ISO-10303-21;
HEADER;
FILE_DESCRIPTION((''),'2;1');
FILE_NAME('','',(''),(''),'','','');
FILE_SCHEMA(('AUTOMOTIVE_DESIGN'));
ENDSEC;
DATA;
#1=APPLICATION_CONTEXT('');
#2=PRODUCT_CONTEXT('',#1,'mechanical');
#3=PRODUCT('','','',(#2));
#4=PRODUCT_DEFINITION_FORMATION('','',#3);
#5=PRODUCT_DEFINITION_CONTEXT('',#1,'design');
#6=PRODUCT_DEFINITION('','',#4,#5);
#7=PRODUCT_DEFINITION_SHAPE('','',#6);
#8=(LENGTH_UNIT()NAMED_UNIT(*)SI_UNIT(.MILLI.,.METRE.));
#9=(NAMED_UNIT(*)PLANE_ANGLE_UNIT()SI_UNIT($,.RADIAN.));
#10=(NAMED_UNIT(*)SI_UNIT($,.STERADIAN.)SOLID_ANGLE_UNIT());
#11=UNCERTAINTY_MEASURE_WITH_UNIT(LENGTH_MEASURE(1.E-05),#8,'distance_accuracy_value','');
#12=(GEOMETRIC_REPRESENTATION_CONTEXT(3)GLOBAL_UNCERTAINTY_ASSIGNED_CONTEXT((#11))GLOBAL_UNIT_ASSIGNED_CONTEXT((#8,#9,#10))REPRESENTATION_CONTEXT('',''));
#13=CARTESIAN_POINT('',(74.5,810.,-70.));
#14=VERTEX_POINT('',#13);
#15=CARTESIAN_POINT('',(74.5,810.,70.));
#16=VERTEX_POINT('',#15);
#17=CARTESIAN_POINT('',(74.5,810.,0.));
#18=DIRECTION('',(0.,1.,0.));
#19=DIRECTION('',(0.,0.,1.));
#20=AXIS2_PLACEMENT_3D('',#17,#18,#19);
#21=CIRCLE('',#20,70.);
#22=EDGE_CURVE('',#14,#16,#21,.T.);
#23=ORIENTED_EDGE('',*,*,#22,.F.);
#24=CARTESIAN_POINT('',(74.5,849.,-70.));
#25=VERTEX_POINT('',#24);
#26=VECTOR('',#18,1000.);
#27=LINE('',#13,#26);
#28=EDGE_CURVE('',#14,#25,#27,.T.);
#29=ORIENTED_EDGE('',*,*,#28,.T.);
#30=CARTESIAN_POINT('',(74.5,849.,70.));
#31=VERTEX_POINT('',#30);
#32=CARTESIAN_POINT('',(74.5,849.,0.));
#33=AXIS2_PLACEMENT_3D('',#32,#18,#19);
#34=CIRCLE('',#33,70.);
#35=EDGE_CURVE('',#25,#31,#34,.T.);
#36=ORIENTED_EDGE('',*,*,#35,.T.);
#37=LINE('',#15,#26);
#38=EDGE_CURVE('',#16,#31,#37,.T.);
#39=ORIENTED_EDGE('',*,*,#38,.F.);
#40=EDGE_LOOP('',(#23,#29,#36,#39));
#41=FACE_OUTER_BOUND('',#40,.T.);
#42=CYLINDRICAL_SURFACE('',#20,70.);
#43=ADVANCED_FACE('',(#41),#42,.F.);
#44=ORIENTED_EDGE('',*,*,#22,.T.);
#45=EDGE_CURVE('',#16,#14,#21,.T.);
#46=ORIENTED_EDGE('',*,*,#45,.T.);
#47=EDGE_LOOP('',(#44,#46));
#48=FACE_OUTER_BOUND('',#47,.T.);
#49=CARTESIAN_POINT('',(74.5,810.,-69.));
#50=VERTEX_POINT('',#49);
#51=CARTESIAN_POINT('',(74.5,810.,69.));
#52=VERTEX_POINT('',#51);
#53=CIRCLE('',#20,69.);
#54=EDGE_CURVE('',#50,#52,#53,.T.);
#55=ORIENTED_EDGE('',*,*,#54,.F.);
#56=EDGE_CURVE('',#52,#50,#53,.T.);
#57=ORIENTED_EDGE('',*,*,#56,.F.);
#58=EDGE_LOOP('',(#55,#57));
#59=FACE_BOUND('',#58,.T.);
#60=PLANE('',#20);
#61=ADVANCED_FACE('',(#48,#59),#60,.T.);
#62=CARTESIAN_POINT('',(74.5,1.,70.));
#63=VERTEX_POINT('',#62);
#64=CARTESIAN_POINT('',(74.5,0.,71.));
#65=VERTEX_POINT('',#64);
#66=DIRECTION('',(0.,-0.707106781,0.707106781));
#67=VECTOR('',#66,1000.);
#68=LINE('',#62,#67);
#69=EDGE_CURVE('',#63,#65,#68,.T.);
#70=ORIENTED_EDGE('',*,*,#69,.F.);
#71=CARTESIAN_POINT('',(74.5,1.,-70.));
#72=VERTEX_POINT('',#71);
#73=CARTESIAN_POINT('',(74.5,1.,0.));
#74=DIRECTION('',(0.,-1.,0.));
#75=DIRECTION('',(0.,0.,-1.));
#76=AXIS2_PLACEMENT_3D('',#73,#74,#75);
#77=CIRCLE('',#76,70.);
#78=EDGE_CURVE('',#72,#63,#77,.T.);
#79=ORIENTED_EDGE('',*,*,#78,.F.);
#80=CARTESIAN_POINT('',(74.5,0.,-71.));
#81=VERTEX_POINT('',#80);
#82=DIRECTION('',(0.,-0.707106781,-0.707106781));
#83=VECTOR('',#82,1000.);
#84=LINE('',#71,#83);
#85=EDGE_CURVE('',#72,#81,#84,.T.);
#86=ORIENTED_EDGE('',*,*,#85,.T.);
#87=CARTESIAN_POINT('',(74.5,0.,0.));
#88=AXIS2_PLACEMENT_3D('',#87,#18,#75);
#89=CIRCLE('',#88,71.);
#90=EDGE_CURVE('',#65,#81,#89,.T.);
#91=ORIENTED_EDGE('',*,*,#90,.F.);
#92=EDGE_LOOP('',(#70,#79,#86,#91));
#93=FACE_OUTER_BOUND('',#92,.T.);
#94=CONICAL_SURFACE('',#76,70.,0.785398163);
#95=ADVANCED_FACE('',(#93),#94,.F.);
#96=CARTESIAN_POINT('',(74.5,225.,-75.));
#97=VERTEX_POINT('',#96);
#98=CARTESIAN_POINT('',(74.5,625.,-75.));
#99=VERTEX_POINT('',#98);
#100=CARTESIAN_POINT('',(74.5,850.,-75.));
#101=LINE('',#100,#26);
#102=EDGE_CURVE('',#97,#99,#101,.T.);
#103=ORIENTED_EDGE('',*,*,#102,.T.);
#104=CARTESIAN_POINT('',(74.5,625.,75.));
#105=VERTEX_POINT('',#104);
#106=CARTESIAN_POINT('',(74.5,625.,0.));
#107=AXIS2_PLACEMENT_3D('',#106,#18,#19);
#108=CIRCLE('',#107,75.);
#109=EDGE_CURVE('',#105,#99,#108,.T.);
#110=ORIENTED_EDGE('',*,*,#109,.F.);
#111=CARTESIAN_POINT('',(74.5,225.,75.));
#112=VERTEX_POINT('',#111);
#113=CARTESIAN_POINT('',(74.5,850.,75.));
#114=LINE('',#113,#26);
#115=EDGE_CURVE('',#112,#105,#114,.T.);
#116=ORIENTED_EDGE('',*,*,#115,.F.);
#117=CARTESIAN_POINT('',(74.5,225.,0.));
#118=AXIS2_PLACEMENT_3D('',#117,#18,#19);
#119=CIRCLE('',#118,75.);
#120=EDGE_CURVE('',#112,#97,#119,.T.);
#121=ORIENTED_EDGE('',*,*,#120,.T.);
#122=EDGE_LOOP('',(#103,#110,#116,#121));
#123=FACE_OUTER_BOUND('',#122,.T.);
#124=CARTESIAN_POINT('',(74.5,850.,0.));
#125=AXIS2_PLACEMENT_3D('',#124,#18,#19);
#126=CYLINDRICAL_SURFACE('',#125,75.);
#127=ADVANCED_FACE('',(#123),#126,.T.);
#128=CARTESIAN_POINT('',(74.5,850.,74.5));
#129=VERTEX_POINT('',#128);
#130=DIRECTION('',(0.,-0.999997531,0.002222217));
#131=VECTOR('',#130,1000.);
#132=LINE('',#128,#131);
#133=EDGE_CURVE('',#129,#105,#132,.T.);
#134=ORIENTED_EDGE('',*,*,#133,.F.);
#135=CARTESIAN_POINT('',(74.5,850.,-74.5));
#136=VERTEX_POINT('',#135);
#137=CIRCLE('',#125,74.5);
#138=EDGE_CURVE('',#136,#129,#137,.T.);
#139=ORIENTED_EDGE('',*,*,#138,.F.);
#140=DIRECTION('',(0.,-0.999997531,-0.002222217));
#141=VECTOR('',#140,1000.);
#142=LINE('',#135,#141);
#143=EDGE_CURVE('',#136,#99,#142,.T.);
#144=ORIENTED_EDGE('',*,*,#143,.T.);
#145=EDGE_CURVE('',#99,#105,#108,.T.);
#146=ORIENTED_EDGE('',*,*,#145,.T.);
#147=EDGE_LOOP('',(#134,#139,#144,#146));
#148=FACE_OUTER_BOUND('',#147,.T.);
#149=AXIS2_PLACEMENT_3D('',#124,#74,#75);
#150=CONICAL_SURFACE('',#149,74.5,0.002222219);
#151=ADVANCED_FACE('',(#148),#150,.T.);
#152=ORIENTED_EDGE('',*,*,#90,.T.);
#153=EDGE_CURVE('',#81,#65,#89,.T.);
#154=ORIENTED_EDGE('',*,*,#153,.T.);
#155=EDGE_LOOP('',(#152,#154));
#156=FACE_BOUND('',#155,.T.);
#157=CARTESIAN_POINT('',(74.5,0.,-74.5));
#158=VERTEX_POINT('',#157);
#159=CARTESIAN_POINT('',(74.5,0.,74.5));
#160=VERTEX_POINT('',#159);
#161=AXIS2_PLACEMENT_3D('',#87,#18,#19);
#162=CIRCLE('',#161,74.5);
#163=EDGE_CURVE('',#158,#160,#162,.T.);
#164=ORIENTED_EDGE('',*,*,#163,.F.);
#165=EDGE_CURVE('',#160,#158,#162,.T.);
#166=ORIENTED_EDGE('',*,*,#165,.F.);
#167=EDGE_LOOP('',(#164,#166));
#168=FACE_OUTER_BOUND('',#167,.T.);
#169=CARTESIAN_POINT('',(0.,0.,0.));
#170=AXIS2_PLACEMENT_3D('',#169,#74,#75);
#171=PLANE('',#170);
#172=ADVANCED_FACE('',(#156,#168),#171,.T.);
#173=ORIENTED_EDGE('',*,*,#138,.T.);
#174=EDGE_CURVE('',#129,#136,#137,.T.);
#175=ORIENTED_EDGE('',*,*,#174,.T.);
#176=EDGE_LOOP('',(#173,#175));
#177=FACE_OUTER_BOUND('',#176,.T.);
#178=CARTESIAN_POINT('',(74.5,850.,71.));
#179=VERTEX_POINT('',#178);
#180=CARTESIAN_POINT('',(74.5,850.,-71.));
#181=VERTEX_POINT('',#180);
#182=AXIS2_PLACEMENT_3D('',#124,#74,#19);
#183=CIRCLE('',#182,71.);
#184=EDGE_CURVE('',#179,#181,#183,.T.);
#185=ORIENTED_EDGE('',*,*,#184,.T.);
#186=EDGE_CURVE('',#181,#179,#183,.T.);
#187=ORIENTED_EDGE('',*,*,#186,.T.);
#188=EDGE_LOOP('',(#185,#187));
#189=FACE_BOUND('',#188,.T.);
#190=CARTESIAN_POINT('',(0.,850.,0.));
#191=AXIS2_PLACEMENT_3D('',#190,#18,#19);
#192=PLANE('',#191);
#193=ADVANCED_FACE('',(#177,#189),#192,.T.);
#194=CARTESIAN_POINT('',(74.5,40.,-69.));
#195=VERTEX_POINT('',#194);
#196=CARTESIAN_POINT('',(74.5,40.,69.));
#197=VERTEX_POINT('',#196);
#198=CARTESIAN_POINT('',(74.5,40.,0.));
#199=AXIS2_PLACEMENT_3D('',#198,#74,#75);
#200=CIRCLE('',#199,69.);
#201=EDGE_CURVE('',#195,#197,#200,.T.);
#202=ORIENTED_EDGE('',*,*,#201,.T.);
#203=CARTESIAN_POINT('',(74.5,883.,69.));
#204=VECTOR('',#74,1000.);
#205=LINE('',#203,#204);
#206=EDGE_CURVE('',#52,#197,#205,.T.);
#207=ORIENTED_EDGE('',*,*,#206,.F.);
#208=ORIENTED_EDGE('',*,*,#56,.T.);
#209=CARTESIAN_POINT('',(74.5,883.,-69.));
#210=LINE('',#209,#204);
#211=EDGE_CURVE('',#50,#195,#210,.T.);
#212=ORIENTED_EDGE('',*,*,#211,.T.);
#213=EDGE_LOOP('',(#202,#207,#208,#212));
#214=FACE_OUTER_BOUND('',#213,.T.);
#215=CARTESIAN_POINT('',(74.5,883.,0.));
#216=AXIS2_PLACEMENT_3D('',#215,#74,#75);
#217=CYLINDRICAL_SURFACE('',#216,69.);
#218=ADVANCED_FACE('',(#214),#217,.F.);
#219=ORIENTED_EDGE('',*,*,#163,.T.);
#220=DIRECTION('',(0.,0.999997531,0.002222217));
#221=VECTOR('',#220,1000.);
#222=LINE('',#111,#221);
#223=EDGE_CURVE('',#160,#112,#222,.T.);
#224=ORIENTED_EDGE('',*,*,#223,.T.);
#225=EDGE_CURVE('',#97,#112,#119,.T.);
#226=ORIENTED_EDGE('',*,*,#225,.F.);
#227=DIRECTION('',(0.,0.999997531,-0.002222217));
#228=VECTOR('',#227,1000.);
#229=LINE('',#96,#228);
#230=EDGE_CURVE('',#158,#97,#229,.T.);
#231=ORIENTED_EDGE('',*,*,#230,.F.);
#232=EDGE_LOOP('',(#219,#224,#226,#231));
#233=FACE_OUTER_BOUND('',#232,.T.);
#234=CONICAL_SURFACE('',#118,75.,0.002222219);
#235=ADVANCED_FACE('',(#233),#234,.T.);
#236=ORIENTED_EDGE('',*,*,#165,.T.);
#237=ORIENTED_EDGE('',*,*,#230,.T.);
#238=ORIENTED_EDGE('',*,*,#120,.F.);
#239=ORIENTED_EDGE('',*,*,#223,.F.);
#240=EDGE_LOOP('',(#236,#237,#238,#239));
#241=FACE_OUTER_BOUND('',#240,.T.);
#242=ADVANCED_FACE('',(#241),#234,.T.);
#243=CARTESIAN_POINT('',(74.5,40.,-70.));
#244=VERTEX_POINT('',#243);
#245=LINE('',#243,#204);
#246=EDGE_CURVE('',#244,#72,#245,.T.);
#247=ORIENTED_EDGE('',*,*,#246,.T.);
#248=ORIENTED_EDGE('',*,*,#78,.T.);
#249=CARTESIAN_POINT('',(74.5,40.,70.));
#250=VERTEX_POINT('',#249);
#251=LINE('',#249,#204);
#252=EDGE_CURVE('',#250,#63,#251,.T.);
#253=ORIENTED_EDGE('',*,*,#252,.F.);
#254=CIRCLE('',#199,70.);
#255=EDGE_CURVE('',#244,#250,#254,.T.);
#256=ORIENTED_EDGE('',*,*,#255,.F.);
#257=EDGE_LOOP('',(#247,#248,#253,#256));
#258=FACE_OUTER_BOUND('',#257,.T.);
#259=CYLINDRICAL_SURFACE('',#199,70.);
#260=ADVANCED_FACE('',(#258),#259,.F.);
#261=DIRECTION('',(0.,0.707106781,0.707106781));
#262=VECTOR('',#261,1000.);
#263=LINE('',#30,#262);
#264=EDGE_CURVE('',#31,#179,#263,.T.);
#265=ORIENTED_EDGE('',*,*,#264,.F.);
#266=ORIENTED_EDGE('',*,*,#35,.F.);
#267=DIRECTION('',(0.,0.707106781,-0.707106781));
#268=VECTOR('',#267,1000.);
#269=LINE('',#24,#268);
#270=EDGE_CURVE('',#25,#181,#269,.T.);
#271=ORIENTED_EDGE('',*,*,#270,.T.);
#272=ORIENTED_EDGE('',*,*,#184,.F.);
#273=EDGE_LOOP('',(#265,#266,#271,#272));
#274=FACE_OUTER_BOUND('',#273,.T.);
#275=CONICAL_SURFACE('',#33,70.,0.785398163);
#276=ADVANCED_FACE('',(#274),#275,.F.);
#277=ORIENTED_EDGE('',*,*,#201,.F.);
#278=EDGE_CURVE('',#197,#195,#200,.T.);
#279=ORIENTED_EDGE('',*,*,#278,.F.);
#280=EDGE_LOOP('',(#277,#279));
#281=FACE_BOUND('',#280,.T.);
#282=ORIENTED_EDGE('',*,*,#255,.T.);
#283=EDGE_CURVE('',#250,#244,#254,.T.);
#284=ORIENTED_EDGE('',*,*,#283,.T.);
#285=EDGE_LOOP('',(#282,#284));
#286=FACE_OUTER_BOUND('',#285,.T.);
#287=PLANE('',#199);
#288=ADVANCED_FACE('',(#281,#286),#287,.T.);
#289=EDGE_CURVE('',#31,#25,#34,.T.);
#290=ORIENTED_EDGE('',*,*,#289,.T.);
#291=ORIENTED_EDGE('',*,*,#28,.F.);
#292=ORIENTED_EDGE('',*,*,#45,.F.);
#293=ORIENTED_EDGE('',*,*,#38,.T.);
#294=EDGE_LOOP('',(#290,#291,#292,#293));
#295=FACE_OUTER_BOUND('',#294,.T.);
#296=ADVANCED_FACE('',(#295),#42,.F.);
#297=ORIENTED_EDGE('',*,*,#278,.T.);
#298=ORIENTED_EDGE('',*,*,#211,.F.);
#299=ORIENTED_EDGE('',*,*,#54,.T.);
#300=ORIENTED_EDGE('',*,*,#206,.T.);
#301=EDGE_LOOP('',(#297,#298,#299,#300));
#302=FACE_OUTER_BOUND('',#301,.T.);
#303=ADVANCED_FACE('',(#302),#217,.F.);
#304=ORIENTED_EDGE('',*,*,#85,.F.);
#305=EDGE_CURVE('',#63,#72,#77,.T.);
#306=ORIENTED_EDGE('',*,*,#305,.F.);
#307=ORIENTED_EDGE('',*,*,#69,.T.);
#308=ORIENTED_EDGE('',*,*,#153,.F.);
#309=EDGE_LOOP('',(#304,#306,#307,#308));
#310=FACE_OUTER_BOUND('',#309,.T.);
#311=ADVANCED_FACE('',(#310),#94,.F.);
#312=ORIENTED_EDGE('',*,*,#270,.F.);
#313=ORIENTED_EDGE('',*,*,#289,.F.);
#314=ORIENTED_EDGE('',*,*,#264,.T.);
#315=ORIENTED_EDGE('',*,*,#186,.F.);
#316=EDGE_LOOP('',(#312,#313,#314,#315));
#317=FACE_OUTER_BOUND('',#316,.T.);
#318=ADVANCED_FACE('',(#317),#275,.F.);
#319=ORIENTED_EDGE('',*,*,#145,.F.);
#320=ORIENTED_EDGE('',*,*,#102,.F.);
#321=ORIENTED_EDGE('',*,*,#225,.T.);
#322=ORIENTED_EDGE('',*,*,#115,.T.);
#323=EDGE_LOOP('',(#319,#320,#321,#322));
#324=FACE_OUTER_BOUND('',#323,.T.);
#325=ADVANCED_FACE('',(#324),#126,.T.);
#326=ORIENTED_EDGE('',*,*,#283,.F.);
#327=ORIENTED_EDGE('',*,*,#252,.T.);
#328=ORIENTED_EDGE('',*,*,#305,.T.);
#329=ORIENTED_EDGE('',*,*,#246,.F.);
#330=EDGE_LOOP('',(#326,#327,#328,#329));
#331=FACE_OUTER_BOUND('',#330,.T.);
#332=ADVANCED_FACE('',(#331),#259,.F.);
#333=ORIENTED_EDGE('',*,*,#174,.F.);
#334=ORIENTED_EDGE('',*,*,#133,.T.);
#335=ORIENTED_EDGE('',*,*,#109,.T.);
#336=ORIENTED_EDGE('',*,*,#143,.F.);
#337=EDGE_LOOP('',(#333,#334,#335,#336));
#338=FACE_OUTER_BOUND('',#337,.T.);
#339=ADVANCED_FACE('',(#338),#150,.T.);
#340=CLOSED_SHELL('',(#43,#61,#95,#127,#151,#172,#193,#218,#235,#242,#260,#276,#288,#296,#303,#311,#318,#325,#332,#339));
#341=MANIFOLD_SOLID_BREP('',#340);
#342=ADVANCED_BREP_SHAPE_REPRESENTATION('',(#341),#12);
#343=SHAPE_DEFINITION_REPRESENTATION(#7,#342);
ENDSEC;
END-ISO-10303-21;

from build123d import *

# Parameters (mm, degrees)
SKETCH_2_R          = 70
CUT_EXTRUDE_1_DEPTH = 40
CUT_EXTRUDE_START   = -40
SKETCH_3_R          = 70
CUT_EXTRUDE_2_DEPTH = 40
SKETCH_4_R          = 69
CUT_EXTRUDE_3_DEPTH = 843
CHAMFER_1_SIZE      = 1


with BuildPart() as part:
    # 草图1 → 旋转1 (revolve)
    with BuildSketch(Plane.XY, mode=Mode.PRIVATE) as revolve_1_sk:
        Polygon((0, 0), (-0.5, 225), (-0.5, 625), (0, 850), (74.5, 850), (74.5, 0), align=None)
    revolve(revolve_1_sk.sketch.rotate(Axis((74.5, 850, 0), (0, -1, 0)), 270), axis=Axis((74.5, 850, 0), (0, -1, 0)))

    # 草图2 → 切除-拉伸1 (cut)
    with BuildSketch(Plane(origin=(0, 850, 0), x_dir=(1, 0, 0), z_dir=(0, 1, 0))):
        with Locations(Location((74.5, 0, 0), (0, 0, 270))):
            Circle(SKETCH_2_R)
    extrude(amount=-CUT_EXTRUDE_1_DEPTH, mode=Mode.SUBTRACT)

    # 草图3 → 切除-拉伸2 (cut)
    with BuildSketch(Plane.XZ.offset(CUT_EXTRUDE_START)):
        with Locations(Location((74.5, 0, 0), (0, 0, 90))):
            Circle(SKETCH_3_R)
    extrude(amount=CUT_EXTRUDE_2_DEPTH, mode=Mode.SUBTRACT)

    # 草图4 → 切除-拉伸3 (cut)
    with BuildSketch(Plane.XZ.offset(-40)):
        with Locations(Location((74.5, 0, 0), (0, 0, 270))):
            Circle(SKETCH_4_R)
    extrude(amount=-CUT_EXTRUDE_3_DEPTH, mode=Mode.SUBTRACT)

    # 倒角1
    chamfer_1_edges = [part.edges().sort_by_distance(p)[0] for p in [
        (74.5, 850, -70),
        (74.5, 0, -70),
    ]]
    chamfer(chamfer_1_edges, length=CHAMFER_1_SIZE)


solid = part.part
